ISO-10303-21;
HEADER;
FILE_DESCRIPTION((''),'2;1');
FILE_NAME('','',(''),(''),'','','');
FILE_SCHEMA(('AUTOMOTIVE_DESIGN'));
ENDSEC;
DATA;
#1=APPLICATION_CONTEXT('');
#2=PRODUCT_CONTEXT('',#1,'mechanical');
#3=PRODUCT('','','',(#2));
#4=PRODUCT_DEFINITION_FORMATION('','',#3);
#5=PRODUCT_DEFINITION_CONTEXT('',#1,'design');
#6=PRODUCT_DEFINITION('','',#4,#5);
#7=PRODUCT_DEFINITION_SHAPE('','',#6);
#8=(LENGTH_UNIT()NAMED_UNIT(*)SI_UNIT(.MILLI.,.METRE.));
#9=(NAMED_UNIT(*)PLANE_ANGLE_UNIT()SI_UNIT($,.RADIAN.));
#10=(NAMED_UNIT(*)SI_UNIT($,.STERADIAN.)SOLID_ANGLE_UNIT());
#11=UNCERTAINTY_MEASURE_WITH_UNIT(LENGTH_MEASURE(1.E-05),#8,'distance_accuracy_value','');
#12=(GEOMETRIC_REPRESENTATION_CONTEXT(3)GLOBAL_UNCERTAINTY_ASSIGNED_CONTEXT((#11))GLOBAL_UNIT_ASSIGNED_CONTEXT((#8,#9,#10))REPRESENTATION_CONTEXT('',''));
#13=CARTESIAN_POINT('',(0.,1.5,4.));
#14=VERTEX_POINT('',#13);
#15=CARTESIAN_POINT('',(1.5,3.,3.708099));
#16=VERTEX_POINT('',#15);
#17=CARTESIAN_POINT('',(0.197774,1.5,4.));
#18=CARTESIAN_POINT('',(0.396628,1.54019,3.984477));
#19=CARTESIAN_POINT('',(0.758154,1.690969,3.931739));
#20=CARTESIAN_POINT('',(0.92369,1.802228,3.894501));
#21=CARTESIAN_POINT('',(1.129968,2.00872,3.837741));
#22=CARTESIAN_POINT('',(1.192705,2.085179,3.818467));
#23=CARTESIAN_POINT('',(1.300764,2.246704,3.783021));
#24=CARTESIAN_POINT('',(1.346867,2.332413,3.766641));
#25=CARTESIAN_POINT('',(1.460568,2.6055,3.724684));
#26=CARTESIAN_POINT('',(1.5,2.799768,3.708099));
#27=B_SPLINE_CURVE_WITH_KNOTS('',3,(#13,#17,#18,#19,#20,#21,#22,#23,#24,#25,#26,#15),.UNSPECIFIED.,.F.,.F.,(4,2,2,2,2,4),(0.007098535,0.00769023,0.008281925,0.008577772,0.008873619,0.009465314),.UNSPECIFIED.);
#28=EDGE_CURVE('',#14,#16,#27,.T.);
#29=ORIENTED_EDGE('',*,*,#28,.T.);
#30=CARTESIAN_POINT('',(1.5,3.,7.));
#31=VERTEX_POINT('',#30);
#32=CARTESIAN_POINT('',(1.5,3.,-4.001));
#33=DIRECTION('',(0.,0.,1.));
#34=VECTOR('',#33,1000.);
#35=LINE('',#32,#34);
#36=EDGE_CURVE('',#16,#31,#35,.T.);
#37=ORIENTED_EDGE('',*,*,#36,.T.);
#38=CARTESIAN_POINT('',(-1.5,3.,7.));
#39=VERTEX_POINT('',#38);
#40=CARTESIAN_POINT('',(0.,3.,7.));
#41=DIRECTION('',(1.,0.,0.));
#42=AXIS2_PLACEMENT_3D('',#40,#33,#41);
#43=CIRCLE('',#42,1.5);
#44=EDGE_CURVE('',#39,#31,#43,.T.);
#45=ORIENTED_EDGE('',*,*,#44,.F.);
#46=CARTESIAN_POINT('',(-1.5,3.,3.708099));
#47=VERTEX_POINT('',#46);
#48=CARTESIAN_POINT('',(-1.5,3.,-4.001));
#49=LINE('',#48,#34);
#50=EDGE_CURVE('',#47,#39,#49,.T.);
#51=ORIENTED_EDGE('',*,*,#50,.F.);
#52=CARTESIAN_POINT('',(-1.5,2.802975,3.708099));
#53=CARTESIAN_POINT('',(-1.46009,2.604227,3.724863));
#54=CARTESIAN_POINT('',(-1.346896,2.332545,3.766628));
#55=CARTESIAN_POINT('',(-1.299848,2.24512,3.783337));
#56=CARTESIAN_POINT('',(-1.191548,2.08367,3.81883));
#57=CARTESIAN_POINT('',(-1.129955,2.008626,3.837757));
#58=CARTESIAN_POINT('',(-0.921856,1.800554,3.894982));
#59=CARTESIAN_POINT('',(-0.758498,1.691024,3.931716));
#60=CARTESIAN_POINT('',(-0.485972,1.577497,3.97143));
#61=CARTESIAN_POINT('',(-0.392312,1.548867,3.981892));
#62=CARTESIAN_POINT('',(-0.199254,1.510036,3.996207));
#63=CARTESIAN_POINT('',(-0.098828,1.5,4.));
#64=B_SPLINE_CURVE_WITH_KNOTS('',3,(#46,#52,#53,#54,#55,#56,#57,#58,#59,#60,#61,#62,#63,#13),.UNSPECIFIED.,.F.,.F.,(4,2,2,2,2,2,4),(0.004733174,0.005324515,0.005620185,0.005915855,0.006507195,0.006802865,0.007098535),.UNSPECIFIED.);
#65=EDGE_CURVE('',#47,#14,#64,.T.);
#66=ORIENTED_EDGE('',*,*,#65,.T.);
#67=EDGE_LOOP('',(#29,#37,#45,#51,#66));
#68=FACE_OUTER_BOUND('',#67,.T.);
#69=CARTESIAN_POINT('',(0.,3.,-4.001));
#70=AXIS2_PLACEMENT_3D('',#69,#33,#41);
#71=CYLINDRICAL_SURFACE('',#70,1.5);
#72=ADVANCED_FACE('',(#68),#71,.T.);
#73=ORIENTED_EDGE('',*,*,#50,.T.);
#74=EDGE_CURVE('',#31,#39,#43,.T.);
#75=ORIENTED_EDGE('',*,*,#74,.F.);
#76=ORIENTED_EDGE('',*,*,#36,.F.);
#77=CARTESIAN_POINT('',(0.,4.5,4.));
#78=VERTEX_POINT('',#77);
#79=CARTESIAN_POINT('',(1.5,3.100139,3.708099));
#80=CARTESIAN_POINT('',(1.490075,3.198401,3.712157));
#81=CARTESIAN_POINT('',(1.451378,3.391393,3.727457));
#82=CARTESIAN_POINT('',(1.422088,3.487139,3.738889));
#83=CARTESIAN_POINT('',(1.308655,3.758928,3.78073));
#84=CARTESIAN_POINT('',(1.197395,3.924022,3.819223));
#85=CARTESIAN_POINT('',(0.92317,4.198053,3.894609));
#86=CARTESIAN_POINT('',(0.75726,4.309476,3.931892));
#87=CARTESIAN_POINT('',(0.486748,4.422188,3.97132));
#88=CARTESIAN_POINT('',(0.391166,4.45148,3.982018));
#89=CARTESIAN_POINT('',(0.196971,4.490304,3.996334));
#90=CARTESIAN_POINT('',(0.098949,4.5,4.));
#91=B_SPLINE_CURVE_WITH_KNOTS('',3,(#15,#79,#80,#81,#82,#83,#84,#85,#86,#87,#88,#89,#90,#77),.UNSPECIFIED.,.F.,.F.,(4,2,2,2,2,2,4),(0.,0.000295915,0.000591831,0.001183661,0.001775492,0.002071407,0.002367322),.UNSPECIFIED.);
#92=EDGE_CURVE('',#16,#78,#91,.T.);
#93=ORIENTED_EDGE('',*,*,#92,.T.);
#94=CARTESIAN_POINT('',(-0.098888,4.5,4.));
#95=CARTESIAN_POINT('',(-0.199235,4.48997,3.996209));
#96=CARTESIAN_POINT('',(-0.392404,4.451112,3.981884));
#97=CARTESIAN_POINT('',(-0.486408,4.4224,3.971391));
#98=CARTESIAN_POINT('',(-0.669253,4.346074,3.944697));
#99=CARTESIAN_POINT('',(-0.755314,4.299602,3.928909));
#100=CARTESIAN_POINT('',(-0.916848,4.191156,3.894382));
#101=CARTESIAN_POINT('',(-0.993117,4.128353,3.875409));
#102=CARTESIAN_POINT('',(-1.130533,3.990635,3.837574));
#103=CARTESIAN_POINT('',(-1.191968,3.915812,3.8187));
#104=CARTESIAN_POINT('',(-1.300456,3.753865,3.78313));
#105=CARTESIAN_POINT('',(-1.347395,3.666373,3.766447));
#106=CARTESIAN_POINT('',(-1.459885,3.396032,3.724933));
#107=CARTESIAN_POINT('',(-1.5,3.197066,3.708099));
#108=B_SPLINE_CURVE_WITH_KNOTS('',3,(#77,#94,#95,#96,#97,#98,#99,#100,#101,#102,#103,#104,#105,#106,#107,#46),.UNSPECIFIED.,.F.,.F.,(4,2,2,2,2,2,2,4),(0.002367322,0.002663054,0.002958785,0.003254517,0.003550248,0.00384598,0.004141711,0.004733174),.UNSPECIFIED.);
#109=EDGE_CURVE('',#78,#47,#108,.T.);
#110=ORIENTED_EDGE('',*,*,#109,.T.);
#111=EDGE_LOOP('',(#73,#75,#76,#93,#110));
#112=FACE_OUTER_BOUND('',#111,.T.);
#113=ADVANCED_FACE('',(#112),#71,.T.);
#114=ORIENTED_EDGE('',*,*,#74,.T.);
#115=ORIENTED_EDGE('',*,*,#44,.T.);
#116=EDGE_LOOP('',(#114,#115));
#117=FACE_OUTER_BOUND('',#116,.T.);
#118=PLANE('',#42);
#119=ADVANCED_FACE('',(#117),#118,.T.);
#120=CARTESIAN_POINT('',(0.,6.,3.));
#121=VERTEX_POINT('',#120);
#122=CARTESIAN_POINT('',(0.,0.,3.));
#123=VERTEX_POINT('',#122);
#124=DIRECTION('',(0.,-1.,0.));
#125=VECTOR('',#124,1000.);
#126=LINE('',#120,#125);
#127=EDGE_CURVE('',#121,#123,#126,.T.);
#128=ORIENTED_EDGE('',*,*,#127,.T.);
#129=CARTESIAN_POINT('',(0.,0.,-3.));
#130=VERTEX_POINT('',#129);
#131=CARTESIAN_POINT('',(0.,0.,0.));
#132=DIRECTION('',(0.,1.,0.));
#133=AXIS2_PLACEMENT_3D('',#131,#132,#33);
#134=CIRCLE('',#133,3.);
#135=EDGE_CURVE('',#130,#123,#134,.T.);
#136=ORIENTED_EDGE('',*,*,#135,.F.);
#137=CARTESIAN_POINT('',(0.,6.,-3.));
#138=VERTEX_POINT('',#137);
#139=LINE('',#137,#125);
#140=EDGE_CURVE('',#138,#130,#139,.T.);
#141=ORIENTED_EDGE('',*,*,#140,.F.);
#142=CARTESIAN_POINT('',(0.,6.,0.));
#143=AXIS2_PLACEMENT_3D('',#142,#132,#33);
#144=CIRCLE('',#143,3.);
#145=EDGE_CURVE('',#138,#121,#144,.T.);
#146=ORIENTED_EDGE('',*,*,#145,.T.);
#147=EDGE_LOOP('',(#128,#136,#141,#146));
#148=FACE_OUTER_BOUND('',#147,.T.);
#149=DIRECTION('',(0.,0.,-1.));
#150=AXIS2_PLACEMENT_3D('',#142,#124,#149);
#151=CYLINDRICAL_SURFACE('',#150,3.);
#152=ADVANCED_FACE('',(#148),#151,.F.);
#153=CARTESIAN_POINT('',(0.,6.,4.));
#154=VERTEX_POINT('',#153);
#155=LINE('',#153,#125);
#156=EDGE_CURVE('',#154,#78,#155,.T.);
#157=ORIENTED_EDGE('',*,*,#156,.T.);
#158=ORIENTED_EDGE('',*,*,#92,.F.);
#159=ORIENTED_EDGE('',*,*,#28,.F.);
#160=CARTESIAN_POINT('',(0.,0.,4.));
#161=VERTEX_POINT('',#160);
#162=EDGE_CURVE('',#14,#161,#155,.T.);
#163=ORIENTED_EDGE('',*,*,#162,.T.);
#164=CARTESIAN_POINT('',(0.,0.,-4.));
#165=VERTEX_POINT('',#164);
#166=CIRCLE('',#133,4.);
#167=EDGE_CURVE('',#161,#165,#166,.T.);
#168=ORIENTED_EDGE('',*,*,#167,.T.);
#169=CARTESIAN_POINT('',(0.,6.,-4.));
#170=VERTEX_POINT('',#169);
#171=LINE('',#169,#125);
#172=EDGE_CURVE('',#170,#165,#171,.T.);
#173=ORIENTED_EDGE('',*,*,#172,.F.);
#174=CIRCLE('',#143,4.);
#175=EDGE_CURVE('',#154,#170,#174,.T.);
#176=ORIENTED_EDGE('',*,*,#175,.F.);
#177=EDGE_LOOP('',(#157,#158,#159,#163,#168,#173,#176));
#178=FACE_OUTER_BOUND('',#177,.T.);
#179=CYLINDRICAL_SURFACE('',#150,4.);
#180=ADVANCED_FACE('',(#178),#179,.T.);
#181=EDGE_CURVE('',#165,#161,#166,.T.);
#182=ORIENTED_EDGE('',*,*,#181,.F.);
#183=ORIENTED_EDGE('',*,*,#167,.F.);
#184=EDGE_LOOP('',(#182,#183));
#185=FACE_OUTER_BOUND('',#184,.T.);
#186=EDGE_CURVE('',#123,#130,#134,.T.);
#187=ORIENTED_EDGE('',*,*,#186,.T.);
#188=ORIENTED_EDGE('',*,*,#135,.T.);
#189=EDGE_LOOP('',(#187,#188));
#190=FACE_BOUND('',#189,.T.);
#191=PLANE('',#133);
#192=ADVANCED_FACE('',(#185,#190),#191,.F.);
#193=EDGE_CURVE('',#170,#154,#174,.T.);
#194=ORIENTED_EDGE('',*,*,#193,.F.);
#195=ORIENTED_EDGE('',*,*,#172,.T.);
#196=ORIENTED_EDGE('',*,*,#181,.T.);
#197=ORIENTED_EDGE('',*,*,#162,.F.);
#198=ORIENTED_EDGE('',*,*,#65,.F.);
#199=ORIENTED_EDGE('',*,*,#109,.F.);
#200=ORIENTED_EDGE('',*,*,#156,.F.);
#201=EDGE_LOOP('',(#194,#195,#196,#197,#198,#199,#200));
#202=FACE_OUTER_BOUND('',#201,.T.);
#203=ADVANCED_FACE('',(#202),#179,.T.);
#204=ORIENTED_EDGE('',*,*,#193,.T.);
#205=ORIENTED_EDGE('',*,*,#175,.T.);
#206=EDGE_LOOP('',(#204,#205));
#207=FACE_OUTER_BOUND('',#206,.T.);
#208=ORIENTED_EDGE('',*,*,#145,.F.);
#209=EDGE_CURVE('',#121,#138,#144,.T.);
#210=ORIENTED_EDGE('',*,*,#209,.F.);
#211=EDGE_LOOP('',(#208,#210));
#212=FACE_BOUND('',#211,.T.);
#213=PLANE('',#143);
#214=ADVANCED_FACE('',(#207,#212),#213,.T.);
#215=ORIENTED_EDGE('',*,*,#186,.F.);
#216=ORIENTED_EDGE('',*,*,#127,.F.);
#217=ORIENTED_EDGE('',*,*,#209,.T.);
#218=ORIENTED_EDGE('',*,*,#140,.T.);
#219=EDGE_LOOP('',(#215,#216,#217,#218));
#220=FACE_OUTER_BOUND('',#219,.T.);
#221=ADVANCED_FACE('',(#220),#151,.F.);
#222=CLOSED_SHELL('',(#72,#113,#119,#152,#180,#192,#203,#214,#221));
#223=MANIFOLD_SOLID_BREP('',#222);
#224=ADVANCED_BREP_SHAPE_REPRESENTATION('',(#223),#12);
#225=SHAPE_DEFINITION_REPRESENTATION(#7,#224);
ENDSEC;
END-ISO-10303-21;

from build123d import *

# Parameters (mm, degrees)
SKETCH1_R                = 4
SKETCH1_R_2              = 3
BOSS_EXTRUDE1_DEPTH      = 6
BOSS_EXTRUDE2_REACH      = 15.153
BOSS_EXTRUDE2_END_RADIUS = 4
SKETCH2_R                = 1.5


with BuildPart() as part:
    # Sketch1 → Boss-Extrude1 (new body)
    with BuildSketch(Plane(origin=(0, 0, 0), x_dir=(1, 0, 0), z_dir=(0, 1, 0))):
        with Locations(Location((0, 0, 0), (0, 0, 270))):
            Circle(SKETCH1_R)
        with Locations(Location((0, 0, 0), (0, 0, 270))):
            Circle(SKETCH1_R_2, mode=Mode.SUBTRACT)
    extrude(amount=BOSS_EXTRUDE1_DEPTH)

    # Boss-Extrude2: up to this cylinder (the profile starts outside it)
    boss_extrude2_end = Plane(origin=(0, 3, 0), z_dir=(0, -1, 0)) * Cylinder(BOSS_EXTRUDE2_END_RADIUS, 39.306, mode=Mode.PRIVATE)
    # Sketch2 → Boss-Extrude2 (add, up to the surface)
    with BuildSketch(Plane.XY.offset(7), mode=Mode.PRIVATE) as boss_extrude2_sk1:
        with Locations((0, 3)):
            Circle(SKETCH2_R)
    boss_extrude2_tool1 = extrude(boss_extrude2_sk1.sketch, amount=-BOSS_EXTRUDE2_REACH, mode=Mode.PRIVATE) - boss_extrude2_end
    add(boss_extrude2_tool1.solids().sort_by_distance((0, 3, 7))[0])


solid = part.part
